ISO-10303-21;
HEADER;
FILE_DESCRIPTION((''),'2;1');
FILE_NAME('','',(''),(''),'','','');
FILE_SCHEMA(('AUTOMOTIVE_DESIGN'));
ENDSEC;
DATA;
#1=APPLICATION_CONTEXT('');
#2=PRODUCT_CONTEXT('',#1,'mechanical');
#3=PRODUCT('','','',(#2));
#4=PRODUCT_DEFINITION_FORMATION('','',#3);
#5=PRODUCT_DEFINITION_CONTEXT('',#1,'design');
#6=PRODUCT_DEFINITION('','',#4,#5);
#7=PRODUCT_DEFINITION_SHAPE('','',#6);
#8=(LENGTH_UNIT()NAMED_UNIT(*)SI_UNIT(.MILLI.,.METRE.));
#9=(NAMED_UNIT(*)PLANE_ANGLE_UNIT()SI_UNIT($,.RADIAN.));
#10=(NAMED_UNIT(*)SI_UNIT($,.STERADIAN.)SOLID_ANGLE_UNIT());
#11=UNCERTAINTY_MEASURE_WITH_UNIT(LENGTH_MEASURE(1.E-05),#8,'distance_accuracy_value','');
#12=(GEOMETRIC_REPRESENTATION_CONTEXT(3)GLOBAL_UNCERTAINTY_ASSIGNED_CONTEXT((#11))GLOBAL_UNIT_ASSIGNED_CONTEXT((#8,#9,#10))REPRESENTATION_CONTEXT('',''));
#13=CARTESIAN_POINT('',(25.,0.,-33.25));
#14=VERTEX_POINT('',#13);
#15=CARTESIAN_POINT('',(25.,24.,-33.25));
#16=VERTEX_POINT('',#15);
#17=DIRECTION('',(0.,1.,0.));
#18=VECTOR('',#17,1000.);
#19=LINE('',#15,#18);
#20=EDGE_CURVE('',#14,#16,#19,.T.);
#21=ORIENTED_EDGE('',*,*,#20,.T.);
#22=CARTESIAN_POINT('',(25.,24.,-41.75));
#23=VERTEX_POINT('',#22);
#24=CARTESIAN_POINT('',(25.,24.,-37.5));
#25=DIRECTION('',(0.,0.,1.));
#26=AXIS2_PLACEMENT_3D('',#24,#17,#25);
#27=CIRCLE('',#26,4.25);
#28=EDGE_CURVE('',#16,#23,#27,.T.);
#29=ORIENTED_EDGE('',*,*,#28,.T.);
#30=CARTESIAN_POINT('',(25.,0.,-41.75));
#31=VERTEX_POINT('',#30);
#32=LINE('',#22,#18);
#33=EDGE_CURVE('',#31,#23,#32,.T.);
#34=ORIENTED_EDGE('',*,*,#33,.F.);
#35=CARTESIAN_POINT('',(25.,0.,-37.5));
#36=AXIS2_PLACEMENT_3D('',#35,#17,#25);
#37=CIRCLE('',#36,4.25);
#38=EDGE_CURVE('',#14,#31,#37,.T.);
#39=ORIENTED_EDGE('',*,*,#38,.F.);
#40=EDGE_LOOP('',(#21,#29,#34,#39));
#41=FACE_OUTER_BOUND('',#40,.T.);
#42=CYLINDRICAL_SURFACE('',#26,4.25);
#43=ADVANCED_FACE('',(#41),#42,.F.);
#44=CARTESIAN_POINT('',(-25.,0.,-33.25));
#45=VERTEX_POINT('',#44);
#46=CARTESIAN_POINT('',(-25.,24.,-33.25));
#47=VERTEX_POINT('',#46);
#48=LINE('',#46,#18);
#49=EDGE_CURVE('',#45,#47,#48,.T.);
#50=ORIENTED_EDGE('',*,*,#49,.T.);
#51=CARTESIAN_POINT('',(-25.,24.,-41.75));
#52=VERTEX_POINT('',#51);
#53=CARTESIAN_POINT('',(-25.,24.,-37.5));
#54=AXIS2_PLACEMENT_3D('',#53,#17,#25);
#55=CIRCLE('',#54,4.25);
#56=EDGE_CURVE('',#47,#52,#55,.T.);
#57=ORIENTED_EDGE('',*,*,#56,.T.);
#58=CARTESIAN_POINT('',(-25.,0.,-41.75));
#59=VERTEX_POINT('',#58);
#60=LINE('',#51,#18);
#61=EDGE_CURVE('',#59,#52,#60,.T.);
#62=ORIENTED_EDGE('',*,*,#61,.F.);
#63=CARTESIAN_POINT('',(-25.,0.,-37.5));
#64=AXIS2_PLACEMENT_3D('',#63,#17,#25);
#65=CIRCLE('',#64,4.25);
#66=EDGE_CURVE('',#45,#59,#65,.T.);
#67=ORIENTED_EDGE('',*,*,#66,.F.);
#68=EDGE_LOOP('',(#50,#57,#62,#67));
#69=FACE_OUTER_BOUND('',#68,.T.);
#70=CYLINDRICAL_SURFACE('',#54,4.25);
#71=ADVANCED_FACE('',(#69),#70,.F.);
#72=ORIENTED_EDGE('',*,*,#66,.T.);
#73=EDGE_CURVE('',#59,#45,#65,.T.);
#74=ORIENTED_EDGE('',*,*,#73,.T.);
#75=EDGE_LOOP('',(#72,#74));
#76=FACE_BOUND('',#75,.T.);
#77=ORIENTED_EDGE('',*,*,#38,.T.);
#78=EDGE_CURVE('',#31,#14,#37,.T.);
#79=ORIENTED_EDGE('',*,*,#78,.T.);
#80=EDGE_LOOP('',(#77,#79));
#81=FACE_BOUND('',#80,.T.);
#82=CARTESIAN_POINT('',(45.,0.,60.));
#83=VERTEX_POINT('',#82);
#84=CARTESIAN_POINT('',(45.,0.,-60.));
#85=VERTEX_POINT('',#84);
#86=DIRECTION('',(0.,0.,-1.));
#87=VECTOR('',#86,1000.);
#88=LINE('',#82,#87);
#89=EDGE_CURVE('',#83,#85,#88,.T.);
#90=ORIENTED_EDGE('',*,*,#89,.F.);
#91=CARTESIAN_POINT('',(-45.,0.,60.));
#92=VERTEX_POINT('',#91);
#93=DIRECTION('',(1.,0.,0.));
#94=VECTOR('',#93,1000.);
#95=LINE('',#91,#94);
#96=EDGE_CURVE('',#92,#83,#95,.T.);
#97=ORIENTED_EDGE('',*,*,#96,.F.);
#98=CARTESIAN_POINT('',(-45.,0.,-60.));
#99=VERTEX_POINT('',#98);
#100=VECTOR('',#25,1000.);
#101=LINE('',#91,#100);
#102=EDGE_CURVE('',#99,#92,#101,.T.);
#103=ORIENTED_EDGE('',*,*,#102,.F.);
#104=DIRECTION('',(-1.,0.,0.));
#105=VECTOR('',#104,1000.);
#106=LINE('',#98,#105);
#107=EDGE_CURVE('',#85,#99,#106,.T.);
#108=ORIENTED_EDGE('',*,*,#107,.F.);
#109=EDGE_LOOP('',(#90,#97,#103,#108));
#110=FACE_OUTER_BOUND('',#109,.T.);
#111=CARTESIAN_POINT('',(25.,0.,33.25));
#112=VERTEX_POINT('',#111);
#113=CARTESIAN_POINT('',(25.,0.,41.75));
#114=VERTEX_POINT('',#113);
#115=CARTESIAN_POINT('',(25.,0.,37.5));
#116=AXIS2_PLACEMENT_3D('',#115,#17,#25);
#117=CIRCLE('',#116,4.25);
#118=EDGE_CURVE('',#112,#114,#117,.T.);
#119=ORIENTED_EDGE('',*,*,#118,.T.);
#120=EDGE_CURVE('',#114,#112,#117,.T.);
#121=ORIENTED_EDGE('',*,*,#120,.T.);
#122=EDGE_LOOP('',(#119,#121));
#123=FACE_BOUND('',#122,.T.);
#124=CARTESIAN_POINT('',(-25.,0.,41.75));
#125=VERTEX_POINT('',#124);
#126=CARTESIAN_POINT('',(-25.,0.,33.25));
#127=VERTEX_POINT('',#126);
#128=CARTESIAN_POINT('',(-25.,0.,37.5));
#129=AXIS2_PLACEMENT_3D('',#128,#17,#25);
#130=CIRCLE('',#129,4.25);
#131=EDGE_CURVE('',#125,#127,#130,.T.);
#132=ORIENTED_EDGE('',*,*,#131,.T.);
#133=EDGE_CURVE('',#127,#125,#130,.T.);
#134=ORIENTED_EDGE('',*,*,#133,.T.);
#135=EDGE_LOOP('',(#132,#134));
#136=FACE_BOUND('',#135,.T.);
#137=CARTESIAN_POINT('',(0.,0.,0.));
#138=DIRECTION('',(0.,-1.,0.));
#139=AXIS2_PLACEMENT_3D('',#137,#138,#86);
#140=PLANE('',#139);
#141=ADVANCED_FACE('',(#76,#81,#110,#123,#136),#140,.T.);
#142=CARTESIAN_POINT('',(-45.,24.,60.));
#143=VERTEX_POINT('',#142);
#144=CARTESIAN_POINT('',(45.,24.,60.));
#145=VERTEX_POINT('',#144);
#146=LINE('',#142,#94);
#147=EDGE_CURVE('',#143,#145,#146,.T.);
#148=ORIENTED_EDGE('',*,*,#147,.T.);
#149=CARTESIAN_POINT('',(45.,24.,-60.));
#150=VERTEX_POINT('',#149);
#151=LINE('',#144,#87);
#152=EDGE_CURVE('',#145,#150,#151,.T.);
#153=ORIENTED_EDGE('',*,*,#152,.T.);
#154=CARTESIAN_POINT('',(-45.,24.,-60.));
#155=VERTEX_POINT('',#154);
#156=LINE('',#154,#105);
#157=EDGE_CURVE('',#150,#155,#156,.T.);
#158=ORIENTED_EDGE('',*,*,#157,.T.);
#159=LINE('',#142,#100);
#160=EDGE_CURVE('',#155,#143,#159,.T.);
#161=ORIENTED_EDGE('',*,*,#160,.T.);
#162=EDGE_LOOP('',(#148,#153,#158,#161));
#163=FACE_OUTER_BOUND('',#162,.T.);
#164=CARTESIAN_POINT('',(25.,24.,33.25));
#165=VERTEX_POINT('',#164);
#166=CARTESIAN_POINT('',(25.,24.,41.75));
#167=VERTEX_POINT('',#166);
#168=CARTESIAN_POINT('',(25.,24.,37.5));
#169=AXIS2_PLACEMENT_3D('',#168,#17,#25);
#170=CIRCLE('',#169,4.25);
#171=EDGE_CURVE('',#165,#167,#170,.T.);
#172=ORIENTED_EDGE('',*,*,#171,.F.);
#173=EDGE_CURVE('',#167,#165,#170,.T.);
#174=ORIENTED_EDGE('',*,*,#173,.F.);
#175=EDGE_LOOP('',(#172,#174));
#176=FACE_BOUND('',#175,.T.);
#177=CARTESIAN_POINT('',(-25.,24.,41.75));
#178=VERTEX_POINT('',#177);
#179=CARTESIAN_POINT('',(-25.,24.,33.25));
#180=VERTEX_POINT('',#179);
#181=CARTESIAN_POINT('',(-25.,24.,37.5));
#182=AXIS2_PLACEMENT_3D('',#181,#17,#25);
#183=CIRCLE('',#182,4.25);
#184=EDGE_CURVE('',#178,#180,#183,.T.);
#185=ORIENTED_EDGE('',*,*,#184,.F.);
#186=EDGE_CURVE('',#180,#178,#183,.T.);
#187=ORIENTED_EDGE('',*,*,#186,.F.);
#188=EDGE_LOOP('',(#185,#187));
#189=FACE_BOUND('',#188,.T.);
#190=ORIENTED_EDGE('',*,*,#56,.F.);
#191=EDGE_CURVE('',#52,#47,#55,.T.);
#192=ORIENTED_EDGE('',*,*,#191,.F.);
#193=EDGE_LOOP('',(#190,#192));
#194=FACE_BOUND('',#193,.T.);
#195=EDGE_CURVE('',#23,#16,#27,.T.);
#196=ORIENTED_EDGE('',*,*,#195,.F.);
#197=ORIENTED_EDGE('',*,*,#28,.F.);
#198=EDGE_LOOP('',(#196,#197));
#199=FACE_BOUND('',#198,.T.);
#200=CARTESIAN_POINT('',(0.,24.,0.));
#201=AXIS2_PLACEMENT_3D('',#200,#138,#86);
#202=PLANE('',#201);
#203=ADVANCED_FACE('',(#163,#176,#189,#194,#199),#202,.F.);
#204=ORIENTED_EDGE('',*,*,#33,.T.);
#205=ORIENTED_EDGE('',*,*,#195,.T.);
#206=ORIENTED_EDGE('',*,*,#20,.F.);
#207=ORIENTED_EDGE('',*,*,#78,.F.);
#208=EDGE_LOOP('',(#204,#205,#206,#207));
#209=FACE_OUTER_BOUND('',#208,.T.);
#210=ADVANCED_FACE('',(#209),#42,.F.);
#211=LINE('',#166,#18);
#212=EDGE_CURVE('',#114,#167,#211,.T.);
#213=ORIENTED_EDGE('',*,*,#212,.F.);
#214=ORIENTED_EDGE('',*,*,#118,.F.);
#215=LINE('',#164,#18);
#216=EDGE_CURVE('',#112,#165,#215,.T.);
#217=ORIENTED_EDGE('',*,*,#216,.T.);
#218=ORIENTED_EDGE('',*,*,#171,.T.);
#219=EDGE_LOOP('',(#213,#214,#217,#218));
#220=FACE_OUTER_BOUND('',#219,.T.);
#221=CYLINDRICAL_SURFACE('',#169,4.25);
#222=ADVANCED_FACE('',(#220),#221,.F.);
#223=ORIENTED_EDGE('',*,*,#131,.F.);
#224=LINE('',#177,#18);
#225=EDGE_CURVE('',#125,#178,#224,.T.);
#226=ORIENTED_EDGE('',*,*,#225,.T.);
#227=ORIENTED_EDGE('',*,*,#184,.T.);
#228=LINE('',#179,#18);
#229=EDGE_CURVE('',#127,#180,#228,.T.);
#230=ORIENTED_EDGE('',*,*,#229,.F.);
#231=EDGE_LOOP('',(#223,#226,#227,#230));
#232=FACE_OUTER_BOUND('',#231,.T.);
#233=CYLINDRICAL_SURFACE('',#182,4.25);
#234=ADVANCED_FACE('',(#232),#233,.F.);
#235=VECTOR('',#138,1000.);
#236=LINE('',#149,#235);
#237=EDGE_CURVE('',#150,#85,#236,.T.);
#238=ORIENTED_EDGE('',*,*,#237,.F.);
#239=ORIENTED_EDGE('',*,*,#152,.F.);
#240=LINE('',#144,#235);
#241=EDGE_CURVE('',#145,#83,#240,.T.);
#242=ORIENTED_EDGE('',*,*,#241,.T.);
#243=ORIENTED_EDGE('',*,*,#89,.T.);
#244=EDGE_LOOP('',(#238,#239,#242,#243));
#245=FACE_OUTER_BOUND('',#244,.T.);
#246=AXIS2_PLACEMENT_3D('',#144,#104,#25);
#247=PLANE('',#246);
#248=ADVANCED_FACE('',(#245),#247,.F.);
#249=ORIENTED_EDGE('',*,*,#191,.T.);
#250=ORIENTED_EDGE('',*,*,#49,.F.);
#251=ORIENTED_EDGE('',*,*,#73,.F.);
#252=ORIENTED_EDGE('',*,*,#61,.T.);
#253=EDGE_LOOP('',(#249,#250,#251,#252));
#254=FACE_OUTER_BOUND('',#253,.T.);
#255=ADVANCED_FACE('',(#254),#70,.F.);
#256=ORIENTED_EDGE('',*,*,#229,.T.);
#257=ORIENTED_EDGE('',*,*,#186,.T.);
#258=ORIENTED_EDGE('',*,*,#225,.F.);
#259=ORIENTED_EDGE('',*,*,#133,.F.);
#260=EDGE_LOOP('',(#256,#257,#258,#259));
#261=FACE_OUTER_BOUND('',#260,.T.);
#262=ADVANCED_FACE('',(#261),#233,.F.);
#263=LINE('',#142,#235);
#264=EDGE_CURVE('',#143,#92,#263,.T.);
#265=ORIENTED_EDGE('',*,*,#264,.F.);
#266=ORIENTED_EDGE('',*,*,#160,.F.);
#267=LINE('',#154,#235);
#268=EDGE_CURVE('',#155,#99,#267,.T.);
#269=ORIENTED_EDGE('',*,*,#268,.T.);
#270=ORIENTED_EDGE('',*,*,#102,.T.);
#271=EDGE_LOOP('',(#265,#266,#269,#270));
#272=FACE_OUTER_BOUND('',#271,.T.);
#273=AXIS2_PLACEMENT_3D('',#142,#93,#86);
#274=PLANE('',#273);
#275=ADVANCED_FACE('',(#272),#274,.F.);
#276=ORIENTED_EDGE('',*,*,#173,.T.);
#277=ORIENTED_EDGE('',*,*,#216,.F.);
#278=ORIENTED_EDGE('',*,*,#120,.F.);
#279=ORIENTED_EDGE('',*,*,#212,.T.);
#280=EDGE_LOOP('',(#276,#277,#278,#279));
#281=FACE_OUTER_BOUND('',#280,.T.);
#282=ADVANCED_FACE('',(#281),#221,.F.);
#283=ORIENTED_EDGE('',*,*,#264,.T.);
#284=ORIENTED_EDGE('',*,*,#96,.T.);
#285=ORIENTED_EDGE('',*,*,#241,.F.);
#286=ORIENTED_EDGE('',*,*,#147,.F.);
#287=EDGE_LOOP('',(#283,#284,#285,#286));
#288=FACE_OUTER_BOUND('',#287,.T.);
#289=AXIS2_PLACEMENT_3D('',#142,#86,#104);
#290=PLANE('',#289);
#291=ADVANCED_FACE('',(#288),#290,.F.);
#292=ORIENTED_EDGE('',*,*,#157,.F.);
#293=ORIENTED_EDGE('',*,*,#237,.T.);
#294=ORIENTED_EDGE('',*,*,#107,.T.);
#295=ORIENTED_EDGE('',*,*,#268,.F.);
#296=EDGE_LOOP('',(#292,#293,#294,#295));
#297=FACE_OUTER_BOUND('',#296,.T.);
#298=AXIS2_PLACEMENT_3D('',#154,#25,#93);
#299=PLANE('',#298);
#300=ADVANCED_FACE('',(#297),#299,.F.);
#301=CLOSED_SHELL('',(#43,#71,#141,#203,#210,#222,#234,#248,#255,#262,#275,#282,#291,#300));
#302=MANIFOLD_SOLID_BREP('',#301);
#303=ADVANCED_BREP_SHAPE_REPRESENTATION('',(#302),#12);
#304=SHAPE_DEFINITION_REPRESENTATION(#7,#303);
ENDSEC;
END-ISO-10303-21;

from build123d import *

# Parameters (mm, degrees)
SKETCH_1_W          = 90
SKETCH_1_H          = 120
EXTRUDE_1_DEPTH     = 24
HOLE_WIZARD_M10_1_D = 8.5


with BuildPart() as part:
    # 草图1 → 凸台-拉伸1 (new body)
    with BuildSketch(Plane(origin=(0, 0, 0), x_dir=(1, 0, 0), z_dir=(0, 1, 0))):
        Rectangle(SKETCH_1_W, SKETCH_1_H)
    extrude(amount=EXTRUDE_1_DEPTH)

    # M10 螺纹孔1 (through all)
    with Locations(Plane(origin=(0, 24, 0), x_dir=(1, 0, 0), z_dir=(0, 1, 0))):
        with Locations((-25, -37.5), (-25, 37.5), (25, 37.5), (25, -37.5)):
            Hole(HOLE_WIZARD_M10_1_D / 2)


solid = part.part
